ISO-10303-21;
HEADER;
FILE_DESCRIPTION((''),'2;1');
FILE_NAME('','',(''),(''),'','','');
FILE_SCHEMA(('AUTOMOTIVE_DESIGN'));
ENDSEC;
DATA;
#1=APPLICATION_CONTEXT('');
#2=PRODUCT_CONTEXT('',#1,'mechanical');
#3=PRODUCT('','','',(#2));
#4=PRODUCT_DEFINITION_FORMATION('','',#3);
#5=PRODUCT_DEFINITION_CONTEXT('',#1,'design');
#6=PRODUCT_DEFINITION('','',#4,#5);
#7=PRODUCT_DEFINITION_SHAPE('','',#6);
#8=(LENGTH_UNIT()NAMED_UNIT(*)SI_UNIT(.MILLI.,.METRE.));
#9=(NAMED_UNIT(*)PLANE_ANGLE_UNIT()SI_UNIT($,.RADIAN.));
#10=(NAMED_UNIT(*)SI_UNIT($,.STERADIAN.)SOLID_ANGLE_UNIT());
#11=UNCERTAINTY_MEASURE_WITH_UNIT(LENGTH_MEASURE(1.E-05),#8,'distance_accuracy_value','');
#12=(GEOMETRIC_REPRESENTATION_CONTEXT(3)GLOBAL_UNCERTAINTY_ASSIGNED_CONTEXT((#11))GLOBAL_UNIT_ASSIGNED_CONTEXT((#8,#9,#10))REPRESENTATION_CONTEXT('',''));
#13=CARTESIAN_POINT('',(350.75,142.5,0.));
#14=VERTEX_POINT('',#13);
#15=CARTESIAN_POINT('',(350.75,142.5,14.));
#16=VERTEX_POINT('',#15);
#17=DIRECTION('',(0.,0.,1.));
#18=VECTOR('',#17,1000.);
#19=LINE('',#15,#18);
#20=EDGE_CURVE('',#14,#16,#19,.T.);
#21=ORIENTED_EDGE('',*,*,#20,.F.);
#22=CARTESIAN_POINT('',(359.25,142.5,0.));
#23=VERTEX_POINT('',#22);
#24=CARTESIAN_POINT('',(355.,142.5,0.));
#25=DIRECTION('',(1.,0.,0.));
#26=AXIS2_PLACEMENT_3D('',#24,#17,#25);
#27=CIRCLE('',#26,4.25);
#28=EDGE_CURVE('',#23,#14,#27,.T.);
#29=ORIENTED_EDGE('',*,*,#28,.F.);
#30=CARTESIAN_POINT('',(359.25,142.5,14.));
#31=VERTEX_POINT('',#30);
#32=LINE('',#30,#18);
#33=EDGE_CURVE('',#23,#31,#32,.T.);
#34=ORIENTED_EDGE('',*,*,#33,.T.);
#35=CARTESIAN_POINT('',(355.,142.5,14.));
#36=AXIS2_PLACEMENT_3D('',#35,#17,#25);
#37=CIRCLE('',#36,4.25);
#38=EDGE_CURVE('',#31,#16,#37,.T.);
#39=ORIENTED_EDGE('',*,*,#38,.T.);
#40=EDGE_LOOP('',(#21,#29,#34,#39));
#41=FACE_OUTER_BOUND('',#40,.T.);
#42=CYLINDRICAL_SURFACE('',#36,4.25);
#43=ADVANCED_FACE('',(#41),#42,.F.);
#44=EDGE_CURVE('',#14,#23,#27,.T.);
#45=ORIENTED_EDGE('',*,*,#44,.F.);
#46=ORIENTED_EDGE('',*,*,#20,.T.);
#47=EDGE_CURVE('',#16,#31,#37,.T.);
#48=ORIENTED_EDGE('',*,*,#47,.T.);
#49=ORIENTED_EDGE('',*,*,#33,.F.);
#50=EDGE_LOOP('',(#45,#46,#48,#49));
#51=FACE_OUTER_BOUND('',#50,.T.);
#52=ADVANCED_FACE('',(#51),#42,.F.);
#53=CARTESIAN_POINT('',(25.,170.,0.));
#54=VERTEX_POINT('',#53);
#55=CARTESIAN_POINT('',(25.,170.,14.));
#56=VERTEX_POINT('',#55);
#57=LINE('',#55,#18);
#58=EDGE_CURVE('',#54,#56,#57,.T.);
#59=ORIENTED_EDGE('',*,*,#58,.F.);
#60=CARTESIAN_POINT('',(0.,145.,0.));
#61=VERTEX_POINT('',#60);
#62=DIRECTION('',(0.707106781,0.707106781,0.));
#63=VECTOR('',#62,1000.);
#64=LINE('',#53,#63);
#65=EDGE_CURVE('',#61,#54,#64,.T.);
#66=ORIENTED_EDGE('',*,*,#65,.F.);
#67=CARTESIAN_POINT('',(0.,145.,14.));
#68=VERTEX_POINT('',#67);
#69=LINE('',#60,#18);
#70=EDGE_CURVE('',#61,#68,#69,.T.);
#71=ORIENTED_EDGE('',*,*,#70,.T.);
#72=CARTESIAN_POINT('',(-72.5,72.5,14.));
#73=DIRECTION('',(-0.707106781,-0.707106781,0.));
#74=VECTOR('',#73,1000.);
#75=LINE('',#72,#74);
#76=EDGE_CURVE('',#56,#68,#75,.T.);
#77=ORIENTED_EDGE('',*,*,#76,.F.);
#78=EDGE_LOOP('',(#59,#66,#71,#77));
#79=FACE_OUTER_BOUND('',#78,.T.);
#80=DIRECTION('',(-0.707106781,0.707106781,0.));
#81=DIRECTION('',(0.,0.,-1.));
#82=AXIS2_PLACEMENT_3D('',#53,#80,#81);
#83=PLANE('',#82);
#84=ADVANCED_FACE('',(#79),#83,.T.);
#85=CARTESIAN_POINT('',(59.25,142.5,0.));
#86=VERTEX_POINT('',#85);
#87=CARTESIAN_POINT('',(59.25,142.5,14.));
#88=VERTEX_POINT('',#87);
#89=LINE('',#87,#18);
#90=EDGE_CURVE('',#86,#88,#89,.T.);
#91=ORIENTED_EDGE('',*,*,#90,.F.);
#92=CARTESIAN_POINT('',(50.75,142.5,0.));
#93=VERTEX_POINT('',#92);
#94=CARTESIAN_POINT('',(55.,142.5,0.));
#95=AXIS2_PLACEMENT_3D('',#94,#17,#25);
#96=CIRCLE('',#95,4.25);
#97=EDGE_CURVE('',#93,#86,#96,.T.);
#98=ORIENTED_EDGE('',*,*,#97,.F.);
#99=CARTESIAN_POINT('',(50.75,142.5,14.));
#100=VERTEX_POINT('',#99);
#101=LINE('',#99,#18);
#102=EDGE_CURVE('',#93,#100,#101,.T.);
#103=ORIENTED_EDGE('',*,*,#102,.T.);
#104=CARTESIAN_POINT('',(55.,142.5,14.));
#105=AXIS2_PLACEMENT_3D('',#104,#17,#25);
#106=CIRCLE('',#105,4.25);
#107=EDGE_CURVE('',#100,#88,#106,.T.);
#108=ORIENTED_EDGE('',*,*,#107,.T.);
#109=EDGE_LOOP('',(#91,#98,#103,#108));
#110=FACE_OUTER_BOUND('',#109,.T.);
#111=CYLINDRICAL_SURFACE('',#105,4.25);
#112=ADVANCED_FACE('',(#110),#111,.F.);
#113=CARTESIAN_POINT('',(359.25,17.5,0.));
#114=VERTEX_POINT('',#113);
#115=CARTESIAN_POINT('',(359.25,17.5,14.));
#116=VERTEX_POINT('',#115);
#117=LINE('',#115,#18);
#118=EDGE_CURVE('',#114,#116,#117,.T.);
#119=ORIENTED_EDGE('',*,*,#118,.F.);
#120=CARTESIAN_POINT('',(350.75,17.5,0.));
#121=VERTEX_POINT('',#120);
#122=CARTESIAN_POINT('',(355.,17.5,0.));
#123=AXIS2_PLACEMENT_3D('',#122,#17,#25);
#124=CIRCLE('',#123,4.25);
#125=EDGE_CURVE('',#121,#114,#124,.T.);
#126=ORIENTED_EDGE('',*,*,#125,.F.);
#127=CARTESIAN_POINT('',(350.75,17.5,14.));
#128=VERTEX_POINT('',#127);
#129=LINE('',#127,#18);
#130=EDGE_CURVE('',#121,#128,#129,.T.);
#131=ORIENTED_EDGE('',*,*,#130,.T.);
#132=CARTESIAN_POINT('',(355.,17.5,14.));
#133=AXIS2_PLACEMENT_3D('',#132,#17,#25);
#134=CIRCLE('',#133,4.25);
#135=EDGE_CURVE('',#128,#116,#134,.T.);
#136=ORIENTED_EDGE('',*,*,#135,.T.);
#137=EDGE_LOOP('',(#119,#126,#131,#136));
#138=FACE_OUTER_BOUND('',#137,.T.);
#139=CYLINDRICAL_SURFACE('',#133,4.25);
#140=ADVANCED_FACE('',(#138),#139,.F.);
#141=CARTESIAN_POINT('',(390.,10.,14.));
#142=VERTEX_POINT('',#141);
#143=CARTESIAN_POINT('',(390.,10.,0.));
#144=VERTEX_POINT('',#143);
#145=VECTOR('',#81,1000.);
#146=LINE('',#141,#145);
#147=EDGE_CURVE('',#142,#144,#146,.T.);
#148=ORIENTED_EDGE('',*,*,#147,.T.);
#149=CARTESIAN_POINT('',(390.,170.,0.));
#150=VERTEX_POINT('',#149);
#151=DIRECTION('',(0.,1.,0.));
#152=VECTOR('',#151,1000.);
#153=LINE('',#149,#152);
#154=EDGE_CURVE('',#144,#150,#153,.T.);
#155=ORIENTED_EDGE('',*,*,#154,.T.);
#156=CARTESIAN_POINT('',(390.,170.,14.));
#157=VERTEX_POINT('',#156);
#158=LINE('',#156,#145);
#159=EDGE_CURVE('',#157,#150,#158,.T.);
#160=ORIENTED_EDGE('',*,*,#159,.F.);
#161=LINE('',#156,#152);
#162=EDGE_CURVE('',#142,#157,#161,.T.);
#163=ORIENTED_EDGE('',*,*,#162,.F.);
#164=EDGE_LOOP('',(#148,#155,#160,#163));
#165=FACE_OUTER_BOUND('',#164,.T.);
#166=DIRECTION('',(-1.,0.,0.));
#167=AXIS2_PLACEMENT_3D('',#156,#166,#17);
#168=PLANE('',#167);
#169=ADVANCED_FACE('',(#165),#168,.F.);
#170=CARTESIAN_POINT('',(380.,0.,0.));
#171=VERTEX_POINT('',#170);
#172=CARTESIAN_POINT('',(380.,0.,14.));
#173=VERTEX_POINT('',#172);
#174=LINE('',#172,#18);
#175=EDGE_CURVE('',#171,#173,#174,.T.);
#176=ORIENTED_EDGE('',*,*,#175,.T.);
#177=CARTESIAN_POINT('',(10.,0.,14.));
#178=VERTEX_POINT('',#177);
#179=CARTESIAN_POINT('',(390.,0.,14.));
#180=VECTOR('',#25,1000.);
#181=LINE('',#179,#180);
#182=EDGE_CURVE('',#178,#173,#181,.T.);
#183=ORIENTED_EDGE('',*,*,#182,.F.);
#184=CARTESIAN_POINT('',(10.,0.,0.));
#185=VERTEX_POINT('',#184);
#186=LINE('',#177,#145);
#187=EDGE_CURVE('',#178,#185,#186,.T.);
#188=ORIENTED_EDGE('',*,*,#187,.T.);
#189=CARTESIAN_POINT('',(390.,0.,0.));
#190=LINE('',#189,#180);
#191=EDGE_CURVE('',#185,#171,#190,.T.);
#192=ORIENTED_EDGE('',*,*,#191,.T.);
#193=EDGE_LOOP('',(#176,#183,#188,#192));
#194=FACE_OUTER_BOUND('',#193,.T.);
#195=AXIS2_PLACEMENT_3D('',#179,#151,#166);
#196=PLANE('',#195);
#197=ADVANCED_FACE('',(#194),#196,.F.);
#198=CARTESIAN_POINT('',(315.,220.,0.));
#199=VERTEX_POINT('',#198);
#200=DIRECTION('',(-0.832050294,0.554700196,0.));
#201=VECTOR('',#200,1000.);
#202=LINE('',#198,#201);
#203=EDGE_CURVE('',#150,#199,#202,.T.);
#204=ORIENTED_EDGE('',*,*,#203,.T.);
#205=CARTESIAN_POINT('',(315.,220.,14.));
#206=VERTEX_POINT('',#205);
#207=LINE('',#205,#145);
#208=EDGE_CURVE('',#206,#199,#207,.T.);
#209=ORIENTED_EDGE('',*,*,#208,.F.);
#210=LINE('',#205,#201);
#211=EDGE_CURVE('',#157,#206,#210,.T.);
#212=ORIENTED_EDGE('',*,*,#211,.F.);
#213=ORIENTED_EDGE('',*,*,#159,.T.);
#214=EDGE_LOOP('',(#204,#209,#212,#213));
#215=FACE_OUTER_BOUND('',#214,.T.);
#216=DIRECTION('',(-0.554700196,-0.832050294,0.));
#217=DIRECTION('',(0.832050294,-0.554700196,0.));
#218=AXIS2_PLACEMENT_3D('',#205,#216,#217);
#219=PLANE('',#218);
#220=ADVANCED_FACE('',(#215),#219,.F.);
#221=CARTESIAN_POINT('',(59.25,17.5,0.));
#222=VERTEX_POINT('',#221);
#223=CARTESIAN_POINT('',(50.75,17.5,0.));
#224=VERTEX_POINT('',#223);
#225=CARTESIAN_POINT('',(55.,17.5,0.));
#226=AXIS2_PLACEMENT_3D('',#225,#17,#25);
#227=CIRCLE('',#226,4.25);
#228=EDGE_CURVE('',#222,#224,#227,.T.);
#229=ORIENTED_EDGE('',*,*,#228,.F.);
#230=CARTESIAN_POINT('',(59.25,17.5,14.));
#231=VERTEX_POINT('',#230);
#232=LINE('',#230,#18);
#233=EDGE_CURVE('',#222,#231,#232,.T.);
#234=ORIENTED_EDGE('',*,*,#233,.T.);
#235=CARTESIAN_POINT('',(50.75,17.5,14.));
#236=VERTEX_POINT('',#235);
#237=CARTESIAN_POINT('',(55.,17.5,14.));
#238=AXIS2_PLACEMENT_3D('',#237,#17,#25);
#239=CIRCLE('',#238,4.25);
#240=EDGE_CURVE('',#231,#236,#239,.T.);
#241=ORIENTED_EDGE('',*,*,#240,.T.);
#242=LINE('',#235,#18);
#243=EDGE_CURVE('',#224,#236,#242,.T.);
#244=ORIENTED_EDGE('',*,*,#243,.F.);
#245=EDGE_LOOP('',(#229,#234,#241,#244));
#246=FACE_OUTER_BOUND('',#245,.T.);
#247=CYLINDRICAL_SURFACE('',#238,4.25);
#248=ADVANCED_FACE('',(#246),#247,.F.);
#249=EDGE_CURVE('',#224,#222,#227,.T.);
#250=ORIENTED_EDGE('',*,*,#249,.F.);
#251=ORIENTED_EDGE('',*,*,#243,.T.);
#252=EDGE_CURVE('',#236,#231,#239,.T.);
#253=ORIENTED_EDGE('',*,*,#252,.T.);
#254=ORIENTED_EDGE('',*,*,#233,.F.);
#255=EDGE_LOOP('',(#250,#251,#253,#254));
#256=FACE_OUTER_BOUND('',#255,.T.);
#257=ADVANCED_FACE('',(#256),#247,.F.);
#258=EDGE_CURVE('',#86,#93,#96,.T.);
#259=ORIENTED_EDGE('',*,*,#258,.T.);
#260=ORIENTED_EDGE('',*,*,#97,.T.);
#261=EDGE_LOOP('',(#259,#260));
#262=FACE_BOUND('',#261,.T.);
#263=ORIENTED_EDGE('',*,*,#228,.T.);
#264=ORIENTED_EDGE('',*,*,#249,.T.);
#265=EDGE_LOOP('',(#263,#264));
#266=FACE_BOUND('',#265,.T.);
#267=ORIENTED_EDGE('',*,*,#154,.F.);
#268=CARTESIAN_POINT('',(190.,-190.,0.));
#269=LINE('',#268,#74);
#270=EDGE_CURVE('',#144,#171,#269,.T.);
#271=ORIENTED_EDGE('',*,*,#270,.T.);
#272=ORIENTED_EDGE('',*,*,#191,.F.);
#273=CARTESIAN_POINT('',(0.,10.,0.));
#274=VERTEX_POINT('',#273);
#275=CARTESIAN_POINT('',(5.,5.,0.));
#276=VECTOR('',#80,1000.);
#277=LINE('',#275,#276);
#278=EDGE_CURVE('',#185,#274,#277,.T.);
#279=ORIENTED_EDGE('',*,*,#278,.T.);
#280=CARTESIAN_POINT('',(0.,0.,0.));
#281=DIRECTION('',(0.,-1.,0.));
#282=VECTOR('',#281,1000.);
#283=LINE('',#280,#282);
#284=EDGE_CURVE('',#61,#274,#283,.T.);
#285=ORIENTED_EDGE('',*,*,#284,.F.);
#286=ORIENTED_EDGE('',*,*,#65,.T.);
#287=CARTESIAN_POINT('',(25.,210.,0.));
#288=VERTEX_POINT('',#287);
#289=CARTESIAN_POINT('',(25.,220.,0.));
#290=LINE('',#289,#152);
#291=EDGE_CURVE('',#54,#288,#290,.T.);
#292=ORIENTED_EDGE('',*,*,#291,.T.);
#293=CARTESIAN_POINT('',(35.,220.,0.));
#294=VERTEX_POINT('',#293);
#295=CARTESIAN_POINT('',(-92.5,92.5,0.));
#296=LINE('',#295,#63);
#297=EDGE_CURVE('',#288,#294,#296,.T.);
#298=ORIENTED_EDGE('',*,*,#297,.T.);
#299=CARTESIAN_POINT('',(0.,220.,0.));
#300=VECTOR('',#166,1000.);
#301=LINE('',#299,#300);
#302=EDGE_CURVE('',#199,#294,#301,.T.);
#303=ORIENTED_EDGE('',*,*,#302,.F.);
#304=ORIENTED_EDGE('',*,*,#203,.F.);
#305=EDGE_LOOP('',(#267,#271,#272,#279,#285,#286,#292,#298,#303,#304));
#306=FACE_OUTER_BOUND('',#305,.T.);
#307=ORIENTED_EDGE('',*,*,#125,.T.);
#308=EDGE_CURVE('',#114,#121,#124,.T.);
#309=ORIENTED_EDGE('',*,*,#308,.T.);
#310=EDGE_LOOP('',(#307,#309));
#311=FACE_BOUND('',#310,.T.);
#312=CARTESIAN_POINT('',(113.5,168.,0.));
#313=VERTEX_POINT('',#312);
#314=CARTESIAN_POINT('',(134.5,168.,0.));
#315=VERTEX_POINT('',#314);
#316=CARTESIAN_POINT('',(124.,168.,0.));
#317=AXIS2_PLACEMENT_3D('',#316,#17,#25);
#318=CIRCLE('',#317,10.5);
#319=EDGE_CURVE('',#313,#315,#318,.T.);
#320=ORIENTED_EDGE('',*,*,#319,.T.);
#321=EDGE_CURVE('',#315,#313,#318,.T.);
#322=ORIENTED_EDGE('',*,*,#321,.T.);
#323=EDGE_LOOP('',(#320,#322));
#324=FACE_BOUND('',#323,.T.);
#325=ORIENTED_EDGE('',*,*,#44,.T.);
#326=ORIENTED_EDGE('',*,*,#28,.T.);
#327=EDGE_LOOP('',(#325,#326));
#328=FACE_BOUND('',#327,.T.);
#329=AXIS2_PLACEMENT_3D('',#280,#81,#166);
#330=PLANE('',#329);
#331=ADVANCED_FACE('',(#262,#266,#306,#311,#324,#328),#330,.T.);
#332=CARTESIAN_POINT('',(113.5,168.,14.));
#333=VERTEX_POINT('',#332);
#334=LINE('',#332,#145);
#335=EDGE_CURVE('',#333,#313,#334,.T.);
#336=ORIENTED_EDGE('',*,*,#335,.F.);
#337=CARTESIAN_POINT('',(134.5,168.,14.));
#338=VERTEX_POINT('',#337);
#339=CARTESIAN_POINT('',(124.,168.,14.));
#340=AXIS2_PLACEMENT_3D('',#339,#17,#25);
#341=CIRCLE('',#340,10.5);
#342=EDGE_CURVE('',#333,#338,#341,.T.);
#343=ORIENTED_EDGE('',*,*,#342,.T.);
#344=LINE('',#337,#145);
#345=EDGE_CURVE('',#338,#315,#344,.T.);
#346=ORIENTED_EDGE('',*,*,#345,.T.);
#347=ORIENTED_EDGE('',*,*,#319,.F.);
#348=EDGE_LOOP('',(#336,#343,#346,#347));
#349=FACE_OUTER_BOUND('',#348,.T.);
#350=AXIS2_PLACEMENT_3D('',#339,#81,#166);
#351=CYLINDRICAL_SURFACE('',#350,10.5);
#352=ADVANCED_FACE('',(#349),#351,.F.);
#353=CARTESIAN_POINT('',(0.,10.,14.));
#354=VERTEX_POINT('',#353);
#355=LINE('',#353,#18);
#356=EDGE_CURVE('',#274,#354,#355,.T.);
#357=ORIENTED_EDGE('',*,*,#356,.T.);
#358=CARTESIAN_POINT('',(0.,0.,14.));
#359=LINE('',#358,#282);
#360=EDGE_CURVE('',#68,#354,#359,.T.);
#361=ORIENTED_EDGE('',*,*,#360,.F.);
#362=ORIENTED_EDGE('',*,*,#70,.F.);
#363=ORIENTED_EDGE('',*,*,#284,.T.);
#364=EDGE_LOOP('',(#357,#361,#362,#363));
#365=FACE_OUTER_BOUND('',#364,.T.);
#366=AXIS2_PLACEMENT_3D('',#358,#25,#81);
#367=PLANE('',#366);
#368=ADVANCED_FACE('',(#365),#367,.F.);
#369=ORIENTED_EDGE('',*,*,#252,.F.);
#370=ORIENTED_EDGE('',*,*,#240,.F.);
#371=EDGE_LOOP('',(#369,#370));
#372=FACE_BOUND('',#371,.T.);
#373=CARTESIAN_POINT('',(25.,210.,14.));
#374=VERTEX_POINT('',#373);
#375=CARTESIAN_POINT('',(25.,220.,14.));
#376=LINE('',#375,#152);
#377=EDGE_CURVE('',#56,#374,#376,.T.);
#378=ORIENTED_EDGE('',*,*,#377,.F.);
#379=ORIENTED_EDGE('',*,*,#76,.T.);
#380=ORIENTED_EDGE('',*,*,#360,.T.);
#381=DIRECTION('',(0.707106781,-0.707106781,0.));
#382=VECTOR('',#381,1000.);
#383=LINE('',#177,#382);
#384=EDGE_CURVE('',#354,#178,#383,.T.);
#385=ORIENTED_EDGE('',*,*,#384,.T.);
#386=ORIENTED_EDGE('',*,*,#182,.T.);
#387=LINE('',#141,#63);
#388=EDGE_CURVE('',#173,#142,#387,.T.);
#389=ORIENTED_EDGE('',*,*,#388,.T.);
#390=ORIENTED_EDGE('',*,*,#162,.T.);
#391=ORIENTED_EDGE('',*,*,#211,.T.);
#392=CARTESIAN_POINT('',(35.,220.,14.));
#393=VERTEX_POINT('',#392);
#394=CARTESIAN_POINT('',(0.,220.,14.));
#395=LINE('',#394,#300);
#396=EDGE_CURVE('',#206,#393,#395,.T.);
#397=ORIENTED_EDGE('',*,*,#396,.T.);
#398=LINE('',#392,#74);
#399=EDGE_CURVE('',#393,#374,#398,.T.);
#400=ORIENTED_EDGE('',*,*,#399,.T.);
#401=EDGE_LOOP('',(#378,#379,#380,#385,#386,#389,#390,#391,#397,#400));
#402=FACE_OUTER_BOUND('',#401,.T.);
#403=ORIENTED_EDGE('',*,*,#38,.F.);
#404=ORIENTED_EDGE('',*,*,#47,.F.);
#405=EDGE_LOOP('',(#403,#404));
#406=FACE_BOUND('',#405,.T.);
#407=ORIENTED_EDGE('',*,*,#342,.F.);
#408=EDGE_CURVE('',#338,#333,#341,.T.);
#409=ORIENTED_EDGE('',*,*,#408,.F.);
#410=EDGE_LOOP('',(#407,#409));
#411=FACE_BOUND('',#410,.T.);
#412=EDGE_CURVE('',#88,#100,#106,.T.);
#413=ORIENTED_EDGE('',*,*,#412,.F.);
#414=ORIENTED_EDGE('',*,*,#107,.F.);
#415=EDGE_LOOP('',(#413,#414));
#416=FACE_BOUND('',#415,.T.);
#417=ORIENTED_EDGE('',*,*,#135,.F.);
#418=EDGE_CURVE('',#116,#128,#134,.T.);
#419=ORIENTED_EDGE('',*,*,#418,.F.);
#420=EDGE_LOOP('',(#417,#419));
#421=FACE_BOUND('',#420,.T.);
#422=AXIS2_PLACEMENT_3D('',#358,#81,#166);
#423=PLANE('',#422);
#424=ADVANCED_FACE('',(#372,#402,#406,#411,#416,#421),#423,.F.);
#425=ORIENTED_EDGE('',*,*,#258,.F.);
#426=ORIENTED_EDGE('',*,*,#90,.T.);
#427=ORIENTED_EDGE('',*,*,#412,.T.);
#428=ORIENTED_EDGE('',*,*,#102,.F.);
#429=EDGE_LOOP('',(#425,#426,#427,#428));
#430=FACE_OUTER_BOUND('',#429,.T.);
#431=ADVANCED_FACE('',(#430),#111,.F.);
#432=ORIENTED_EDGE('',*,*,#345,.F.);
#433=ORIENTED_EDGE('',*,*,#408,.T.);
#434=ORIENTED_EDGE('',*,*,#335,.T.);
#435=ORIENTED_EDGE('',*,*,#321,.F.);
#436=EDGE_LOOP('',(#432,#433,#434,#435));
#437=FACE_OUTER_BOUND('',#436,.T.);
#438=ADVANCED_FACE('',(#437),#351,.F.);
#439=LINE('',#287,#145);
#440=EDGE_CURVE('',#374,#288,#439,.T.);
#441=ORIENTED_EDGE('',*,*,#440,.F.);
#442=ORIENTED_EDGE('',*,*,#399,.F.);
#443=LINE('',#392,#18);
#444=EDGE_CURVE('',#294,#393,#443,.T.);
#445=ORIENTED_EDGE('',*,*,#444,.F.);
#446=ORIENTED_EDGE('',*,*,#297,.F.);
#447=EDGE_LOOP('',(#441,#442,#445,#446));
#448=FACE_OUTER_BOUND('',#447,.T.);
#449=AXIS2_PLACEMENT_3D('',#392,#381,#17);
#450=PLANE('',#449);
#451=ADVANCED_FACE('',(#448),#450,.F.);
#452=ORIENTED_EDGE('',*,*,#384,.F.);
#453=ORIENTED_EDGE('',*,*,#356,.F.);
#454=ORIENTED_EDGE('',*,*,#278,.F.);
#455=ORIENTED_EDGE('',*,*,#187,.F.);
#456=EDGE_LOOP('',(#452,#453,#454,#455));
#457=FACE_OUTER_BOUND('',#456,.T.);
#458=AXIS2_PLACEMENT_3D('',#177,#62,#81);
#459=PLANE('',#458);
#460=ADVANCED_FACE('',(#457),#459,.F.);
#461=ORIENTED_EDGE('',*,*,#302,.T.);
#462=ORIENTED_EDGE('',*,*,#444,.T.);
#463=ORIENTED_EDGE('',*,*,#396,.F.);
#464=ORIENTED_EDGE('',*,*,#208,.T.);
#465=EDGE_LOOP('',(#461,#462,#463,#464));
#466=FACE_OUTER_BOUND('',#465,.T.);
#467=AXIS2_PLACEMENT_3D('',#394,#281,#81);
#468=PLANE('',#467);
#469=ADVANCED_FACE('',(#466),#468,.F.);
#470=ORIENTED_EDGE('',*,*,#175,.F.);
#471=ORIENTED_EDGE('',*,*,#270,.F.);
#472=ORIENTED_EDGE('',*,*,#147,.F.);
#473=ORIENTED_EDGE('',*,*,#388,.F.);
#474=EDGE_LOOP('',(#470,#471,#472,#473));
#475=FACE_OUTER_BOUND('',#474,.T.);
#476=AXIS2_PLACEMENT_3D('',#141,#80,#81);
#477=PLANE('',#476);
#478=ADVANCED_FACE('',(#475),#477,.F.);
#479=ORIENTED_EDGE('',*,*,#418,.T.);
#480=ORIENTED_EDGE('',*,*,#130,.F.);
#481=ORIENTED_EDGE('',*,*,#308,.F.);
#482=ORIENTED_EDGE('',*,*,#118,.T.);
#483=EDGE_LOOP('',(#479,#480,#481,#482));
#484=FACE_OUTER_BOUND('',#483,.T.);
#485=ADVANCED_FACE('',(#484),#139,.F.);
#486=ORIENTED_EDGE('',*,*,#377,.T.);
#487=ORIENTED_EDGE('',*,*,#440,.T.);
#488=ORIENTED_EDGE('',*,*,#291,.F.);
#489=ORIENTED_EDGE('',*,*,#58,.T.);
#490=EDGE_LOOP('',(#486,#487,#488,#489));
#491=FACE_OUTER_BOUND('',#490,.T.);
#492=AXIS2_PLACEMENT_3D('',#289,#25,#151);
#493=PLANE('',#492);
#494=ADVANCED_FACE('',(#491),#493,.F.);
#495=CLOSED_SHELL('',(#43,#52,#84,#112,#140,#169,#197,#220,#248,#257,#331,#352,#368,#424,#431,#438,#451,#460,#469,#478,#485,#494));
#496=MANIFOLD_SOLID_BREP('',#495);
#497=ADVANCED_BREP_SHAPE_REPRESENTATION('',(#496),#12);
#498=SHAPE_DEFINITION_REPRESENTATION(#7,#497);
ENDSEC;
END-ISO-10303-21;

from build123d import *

# Parameters (mm, degrees)
SKETCH1_R           = 10.5
BOSS_EXTRUDE1_DEPTH = 14
M10_TAPPED_HOLE1_D  = 8.5
SKETCH4_W           = 25
SKETCH4_H           = 60
CUT_EXTRUDE1_DEPTH  = 448.99107134
CHAMFER1_SIZE       = 10
CUT_EXTRUDE2_DEPTH  = 448.99107134


with BuildPart() as part:
    # Sketch1 → Boss-Extrude1 (new body)
    with BuildSketch(Plane.XY):
        Polygon((0, 220), (315, 220), (390, 170), (390, 0), (0, 0), align=None)
        with Locations((124, 168)):
            Circle(SKETCH1_R, mode=Mode.SUBTRACT)
    extrude(amount=BOSS_EXTRUDE1_DEPTH)

    # M10 Tapped Hole1 (through all)
    with Locations(Plane.XY.offset(14)):
        with Locations((55, 142.5), (55, 17.5), (355, 142.5), (355, 17.5)):
            Hole(M10_TAPPED_HOLE1_D / 2)

    # Sketch4 → Cut-Extrude1 (cut, through all)
    with BuildSketch(Plane.XY.offset(14)):
        with Locations((12.5, 190)):
            Rectangle(SKETCH4_W, SKETCH4_H)
    extrude(amount=-CUT_EXTRUDE1_DEPTH, mode=Mode.SUBTRACT)

    # Chamfer1
    chamfer1_edges = [part.edges().sort_by_distance(p)[0] for p in [
        (25, 220, 7),
        (25, 160, 7),
        (390, 0, 7),
        (0, 0, 7),
    ]]
    chamfer(chamfer1_edges, length=CHAMFER1_SIZE)

    # Sketch5 → Cut-Extrude2 (cut, through all)
    with BuildSketch(Plane.XY.offset(14)):
        Polygon((15, 160), (0, 160), (0, 145), align=None)
    extrude(amount=-CUT_EXTRUDE2_DEPTH, mode=Mode.SUBTRACT)


solid = part.part
